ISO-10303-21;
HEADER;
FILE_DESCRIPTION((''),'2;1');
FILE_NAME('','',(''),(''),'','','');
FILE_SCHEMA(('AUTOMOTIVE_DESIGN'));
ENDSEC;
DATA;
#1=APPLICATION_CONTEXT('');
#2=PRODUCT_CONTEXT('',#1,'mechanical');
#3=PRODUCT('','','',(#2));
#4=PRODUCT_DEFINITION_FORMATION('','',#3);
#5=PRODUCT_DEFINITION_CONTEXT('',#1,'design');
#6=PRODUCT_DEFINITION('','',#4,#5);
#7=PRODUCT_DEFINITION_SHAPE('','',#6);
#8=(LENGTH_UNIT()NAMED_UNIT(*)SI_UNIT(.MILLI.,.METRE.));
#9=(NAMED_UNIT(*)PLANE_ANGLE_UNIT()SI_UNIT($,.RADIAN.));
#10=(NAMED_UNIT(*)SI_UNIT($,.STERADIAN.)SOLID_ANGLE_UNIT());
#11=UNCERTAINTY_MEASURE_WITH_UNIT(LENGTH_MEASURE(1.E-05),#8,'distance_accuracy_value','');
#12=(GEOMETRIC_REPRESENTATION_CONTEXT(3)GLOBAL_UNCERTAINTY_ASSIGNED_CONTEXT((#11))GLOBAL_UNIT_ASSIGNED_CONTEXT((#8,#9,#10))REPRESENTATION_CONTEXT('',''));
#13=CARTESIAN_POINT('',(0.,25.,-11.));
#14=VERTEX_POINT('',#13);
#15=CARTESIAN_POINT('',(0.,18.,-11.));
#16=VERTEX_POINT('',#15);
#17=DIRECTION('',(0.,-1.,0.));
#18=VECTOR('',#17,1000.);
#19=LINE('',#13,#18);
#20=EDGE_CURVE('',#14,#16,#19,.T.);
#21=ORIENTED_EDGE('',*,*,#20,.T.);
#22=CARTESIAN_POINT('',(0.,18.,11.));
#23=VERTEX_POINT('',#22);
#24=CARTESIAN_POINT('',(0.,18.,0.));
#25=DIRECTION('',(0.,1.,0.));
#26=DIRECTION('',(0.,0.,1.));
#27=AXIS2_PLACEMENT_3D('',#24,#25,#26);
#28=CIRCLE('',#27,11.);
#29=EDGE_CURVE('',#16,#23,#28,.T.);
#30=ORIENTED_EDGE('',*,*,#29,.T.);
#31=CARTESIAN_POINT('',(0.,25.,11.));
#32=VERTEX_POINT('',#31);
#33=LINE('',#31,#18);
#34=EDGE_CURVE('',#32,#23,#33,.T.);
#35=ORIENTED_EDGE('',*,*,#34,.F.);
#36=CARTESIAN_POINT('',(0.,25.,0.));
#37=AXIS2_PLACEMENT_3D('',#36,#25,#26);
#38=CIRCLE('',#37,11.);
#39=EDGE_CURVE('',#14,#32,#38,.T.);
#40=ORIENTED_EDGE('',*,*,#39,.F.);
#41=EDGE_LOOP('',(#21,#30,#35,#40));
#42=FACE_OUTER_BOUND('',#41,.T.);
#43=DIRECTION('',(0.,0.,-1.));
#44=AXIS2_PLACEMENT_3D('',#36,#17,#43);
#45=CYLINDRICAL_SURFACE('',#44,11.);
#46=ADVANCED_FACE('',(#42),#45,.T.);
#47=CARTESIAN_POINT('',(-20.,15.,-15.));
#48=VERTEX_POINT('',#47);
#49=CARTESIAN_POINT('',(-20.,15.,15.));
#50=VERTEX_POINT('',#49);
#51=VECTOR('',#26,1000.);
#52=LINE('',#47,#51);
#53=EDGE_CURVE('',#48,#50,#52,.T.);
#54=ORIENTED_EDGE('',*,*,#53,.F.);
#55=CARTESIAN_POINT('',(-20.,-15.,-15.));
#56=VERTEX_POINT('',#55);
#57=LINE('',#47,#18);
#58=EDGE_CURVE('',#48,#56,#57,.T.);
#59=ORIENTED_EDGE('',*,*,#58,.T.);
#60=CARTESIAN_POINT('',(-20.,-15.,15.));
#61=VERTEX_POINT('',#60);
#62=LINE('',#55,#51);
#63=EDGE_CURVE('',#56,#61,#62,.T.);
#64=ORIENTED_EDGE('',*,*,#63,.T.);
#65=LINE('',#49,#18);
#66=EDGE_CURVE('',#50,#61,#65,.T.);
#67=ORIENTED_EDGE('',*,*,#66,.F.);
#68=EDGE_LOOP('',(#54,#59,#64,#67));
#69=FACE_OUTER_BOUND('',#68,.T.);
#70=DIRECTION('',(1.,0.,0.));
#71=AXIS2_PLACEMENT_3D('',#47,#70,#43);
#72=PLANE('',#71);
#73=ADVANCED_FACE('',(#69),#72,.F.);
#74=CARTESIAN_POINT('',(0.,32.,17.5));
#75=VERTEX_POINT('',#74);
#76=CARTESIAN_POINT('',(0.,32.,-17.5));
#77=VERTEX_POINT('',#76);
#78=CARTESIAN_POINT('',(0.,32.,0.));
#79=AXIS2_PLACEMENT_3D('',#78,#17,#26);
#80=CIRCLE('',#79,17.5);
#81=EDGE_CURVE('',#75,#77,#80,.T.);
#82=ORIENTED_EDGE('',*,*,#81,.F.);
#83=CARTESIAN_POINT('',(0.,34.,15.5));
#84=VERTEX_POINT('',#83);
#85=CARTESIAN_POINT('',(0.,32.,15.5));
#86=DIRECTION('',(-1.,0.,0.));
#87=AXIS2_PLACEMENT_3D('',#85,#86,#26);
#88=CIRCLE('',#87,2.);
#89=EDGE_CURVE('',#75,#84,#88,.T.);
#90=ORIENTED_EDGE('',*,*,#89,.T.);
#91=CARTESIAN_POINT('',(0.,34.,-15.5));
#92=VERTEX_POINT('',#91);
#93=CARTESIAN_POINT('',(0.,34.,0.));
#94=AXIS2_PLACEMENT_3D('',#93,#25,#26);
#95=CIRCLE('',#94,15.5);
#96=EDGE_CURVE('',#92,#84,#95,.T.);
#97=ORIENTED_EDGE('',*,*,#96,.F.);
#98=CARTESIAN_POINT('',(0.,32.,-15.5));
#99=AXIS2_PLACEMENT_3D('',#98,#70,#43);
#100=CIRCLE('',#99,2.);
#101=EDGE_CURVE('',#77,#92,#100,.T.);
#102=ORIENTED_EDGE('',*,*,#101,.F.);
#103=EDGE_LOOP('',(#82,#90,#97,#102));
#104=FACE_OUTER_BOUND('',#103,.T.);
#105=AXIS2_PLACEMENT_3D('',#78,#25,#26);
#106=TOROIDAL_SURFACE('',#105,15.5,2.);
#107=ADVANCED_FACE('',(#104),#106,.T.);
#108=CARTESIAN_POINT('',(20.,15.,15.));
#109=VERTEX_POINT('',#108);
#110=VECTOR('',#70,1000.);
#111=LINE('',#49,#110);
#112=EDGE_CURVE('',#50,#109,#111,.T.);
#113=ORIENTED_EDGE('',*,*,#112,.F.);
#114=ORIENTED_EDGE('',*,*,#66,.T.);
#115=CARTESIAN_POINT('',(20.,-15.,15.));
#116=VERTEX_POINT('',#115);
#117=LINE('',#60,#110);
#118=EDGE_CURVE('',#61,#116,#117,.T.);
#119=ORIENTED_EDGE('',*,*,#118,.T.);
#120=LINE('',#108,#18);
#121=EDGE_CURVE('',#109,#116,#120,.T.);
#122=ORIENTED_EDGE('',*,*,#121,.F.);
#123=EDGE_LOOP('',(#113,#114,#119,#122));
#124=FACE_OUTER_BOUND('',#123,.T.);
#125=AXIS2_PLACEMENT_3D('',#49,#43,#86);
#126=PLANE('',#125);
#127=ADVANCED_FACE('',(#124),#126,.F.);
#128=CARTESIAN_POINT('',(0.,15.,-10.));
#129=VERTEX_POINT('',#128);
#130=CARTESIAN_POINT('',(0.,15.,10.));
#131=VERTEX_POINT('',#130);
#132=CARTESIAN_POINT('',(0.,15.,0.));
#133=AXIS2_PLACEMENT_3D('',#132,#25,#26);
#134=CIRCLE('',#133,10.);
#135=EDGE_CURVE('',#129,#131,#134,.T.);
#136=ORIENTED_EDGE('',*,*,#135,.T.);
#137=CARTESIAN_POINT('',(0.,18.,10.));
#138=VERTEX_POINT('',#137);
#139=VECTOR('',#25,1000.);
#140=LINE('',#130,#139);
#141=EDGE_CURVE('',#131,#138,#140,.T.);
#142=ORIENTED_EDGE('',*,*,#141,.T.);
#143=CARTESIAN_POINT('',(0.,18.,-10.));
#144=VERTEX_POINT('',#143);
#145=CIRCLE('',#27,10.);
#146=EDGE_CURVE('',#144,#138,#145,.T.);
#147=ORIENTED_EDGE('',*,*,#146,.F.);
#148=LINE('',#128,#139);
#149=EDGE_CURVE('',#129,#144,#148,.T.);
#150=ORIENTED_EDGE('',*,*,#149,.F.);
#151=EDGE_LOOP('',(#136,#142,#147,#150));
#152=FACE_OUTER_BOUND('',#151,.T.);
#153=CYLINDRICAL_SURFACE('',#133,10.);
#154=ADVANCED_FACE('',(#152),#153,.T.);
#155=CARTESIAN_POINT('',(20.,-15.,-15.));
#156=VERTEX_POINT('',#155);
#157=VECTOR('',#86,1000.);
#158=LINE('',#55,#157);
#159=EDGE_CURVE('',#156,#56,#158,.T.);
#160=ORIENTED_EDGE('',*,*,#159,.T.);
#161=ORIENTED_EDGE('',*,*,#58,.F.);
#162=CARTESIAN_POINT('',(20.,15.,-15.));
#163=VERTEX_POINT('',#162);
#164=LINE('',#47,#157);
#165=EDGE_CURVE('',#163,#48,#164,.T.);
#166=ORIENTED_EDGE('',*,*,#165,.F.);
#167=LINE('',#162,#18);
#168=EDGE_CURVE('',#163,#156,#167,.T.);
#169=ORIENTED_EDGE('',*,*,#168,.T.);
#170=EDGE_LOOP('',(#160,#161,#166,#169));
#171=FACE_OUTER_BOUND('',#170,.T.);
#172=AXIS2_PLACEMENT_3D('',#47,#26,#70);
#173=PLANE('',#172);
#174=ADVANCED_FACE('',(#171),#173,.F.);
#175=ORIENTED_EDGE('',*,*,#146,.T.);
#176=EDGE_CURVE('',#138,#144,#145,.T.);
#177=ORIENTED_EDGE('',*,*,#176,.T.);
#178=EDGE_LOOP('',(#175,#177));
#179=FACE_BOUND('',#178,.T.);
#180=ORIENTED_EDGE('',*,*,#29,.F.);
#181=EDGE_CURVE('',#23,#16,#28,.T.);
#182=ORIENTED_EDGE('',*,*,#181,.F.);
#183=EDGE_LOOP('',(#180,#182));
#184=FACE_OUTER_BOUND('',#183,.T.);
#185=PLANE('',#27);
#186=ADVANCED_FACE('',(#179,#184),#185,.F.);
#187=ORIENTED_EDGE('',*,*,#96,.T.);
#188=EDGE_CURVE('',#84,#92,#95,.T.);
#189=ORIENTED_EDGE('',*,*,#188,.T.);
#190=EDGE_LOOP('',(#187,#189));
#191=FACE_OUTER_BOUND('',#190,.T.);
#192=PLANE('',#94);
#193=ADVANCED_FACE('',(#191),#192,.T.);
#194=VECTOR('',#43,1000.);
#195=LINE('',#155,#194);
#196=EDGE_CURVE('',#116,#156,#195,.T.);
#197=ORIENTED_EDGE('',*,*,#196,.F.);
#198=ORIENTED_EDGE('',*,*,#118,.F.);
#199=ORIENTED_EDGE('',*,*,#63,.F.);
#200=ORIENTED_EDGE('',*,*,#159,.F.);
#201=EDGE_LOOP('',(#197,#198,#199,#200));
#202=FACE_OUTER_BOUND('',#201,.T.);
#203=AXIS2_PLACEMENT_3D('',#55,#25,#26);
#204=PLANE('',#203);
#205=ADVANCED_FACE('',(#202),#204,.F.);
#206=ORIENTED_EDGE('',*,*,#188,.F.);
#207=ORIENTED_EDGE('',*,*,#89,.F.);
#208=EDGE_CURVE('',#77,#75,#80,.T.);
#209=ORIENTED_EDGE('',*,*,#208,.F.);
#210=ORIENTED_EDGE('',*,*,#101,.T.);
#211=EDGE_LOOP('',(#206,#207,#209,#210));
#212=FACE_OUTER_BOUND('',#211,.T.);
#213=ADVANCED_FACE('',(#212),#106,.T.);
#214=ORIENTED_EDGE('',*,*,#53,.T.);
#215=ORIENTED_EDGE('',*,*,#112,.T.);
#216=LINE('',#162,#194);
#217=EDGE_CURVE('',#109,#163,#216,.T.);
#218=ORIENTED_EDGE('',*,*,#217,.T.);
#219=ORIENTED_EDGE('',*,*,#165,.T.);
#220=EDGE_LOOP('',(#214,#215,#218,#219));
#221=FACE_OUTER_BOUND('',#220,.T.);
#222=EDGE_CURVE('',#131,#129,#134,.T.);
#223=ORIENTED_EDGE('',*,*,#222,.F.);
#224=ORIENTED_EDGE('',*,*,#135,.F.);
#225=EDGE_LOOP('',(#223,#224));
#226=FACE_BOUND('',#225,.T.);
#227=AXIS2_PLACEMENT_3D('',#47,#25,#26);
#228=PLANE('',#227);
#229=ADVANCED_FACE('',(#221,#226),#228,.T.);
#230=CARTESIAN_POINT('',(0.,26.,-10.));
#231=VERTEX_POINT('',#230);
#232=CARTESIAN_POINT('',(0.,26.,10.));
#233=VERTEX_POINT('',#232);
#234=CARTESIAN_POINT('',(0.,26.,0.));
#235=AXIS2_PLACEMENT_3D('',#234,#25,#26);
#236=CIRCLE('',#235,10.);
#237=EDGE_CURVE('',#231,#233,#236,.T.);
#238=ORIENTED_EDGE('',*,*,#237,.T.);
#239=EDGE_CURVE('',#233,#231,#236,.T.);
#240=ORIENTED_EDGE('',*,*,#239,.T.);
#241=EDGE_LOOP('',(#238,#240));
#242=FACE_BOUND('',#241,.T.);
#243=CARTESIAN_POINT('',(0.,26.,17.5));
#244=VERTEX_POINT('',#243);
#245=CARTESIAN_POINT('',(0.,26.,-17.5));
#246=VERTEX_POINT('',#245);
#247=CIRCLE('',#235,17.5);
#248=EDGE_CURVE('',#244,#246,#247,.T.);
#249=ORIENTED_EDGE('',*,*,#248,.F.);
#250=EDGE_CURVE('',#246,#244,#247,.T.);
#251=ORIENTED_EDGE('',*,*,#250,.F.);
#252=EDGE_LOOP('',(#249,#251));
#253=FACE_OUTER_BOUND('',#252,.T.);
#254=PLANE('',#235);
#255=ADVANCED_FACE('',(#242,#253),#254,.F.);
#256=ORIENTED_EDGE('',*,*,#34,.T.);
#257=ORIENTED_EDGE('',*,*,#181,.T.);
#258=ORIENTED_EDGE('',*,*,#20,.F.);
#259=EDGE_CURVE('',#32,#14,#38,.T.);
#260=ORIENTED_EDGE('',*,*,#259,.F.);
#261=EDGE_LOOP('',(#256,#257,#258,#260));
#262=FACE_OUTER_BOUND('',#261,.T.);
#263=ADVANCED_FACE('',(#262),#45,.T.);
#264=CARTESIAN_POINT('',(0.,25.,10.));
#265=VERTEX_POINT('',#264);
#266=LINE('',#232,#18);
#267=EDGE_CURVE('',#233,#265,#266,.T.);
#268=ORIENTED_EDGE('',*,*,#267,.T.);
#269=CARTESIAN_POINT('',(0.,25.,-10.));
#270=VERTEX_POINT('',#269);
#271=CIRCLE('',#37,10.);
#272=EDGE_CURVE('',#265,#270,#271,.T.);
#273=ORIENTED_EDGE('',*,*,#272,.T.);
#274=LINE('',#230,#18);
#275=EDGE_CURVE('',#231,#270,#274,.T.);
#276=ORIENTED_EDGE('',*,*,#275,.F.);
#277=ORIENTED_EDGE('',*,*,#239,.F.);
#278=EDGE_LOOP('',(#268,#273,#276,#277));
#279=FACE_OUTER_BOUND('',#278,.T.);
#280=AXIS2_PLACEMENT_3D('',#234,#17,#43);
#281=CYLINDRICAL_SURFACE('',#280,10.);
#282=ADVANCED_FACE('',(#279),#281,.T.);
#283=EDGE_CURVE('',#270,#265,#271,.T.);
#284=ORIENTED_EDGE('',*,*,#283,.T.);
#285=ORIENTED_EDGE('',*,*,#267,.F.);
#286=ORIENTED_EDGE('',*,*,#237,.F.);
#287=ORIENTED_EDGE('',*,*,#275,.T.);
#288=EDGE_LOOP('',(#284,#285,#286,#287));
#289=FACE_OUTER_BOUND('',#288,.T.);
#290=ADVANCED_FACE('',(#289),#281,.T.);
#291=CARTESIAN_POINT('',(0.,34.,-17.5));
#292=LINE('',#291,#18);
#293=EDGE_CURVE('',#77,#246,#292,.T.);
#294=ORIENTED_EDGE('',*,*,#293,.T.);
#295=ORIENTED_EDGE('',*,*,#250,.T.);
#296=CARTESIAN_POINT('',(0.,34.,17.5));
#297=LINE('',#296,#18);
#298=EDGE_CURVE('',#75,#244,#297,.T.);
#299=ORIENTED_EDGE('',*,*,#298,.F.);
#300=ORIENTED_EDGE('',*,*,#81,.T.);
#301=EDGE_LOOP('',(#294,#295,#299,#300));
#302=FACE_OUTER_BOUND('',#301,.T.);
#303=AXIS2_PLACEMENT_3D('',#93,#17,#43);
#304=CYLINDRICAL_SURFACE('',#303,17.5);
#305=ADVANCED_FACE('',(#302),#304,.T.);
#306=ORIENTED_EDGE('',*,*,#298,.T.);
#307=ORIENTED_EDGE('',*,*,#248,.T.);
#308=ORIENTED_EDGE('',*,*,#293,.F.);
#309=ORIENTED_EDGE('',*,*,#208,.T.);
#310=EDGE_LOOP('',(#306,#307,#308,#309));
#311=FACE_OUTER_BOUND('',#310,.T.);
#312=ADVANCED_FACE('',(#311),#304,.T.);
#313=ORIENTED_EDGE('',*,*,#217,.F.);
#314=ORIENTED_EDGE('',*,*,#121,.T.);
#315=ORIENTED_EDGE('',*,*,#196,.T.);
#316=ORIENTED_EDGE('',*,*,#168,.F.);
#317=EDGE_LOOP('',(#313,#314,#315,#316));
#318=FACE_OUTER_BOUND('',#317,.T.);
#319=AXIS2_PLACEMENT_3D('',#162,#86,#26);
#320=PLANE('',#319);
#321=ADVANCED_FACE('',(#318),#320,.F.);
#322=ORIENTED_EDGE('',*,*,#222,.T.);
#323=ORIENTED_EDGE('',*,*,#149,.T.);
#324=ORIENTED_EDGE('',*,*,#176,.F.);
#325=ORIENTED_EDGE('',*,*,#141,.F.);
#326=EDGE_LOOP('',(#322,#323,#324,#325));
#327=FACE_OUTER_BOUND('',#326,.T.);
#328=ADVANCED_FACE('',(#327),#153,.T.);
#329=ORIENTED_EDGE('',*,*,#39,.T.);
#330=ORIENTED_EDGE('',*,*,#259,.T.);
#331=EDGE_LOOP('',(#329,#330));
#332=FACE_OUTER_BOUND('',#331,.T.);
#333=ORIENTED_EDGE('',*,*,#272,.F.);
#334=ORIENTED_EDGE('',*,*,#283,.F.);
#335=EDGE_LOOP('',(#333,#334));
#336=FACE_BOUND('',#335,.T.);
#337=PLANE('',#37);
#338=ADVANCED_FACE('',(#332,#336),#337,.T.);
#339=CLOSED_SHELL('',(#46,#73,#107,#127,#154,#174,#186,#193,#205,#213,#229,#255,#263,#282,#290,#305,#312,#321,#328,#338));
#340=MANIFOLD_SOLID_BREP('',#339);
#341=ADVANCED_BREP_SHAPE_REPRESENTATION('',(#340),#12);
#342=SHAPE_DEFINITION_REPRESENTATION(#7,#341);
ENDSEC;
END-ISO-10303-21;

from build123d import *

# Parameters (mm, degrees)
SKETCH1_W          = 40
SKETCH1_H          = 30
EXTRUDE1_DEPTH     = 15
SKETCH2_R          = 11
EXTRUDE2_DEPTH     = 10
SKETCH3_R          = 10
EXTRUDE3_DEPTH     = 1
SKETCH4_R          = 17.5
EXTRUDE4_DEPTH     = 8
FILLET1_R          = 2
SKETCH5_OUTSIDE_W  = 56.458
SKETCH5_OUTSIDE_H  = 51.458
SKETCH5_OUTSIDE_R  = 10
CUT_EXTRUDE1_DEPTH = 3


with BuildPart() as part:
    # Sketch1 → Extrude1 (new, symmetric)
    with BuildSketch(Plane(origin=(0, 0, 0), x_dir=(1, 0, 0), z_dir=(0, 1, 0))):
        Rectangle(SKETCH1_W, SKETCH1_H)
    extrude(amount=EXTRUDE1_DEPTH, both=True)

    # Sketch2 → Extrude2 (add)
    with BuildSketch(Plane(origin=(0, 15, 0), x_dir=(1, 0, 0), z_dir=(0, 1, 0))):
        with Locations(Location((0, 0, 0), (0, 0, 270))):
            Circle(SKETCH2_R)
    extrude(amount=EXTRUDE2_DEPTH)

    # Sketch3 → Extrude3 (add)
    with BuildSketch(Plane(origin=(0, 25, 0), x_dir=(1, 0, 0), z_dir=(0, 1, 0))):
        with Locations(Location((0, 0, 0), (0, 0, 270))):
            Circle(SKETCH3_R)
    extrude(amount=EXTRUDE3_DEPTH)

    # Sketch4 → Extrude4 (add)
    with BuildSketch(Plane(origin=(0, 26, 0), x_dir=(1, 0, 0), z_dir=(0, 1, 0))):
        with Locations(Location((0, 0, 0), (0, 0, 270))):
            Circle(SKETCH4_R)
    extrude(amount=EXTRUDE4_DEPTH)

    # Fillet1
    fillet1_edges = [part.edges().sort_by_distance(p)[0] for p in [
        (0, 34, -17.5),
    ]]
    fillet(fillet1_edges, radius=FILLET1_R)

    # Sketch5 outside → Cut-Extrude1 (cut)
    with BuildSketch(Plane(origin=(0, 18, 0), x_dir=(-1, 0, 0), z_dir=(0, 1, 0))):
        Rectangle(SKETCH5_OUTSIDE_W, SKETCH5_OUTSIDE_H)
        with Locations(Location((0, 0, 0), (0, 0, 90))):
            Circle(SKETCH5_OUTSIDE_R, mode=Mode.SUBTRACT)
    extrude(amount=-CUT_EXTRUDE1_DEPTH, mode=Mode.SUBTRACT)


solid = part.part
